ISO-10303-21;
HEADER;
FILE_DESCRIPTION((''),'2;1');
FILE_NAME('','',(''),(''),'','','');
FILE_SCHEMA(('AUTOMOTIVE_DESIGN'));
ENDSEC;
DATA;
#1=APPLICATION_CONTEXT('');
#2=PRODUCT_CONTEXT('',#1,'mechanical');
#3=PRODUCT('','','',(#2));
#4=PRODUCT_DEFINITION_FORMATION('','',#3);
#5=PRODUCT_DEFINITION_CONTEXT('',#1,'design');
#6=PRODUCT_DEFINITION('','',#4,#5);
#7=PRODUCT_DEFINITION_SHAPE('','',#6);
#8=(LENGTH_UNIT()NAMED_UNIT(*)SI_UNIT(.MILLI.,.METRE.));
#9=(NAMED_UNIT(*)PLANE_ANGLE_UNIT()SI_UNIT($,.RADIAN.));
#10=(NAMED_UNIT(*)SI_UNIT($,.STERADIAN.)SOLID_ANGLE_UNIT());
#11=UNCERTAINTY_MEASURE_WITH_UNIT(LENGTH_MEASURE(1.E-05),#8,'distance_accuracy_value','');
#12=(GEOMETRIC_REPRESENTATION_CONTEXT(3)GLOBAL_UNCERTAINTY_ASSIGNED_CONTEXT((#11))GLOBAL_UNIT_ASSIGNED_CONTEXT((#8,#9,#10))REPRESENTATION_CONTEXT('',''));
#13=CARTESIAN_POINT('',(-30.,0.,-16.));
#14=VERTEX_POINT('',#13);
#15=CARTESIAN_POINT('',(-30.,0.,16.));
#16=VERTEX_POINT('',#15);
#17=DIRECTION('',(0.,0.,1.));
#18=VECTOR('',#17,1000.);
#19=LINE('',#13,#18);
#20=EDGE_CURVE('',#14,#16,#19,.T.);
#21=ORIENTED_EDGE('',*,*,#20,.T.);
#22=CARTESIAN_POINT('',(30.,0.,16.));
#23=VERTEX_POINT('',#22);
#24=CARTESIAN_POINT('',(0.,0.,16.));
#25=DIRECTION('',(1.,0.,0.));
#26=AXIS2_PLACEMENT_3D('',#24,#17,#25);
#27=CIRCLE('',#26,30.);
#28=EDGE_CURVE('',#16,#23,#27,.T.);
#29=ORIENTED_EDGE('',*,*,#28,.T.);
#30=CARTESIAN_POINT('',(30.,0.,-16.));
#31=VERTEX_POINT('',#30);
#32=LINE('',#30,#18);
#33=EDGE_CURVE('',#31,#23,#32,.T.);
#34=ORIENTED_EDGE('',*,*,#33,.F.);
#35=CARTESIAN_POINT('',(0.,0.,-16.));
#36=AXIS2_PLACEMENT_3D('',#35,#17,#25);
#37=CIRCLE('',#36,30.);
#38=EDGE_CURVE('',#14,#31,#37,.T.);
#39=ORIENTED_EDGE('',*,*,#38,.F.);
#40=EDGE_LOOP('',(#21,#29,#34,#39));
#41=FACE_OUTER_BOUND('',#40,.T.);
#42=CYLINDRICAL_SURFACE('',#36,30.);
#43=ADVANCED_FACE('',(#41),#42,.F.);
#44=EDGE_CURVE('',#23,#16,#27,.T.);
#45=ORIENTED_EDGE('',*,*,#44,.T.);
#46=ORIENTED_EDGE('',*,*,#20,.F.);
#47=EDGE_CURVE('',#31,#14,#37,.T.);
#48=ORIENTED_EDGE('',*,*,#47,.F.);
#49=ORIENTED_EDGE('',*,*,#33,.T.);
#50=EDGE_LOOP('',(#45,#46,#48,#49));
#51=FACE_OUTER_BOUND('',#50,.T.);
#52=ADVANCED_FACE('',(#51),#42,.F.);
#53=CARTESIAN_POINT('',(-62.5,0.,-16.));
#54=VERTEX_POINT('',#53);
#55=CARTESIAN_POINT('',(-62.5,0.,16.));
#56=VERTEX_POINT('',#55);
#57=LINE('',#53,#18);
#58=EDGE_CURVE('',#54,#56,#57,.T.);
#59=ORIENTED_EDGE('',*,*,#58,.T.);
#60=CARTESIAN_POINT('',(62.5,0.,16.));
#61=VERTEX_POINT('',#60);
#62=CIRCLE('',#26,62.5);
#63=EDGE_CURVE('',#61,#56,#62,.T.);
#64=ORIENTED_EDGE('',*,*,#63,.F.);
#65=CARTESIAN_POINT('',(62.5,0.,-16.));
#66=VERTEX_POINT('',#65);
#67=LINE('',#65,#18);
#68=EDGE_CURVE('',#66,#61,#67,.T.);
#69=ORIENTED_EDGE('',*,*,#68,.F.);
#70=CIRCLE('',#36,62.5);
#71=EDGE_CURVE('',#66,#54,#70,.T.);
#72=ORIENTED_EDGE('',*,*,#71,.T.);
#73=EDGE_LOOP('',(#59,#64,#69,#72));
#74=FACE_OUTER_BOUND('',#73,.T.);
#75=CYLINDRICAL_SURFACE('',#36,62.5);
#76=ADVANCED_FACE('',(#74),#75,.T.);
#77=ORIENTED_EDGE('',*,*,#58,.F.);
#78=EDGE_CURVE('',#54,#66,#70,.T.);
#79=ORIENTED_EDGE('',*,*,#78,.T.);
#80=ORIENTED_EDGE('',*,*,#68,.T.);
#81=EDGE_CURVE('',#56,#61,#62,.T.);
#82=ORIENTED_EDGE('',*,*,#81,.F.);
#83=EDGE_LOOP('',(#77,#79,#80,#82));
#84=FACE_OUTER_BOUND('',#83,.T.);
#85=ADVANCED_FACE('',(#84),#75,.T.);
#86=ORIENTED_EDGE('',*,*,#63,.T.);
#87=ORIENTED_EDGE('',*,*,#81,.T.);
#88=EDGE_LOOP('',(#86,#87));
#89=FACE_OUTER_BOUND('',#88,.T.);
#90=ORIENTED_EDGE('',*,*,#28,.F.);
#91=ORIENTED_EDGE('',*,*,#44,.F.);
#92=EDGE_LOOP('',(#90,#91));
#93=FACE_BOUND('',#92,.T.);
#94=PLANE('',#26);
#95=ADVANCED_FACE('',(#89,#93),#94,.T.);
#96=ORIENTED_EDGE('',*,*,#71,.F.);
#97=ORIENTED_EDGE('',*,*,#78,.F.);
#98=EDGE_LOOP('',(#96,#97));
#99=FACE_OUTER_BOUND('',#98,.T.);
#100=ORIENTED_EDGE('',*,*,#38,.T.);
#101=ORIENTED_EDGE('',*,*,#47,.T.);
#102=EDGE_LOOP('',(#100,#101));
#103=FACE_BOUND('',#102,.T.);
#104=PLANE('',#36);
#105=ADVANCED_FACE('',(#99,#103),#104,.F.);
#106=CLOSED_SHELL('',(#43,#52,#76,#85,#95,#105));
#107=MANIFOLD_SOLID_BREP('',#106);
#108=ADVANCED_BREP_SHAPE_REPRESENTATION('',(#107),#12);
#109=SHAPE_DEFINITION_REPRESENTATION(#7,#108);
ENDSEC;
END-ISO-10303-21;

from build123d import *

# Parameters (mm, degrees)
SKETCH_1_R      = 62.5
SKETCH_1_R_2    = 30
EXTRUDE_1_DEPTH = 16


with BuildPart() as part:
    # 草图1 → 凸台-拉伸1 (new, symmetric)
    with BuildSketch(Plane.XY):
        Circle(SKETCH_1_R)
        Circle(SKETCH_1_R_2, mode=Mode.SUBTRACT)
    extrude(amount=EXTRUDE_1_DEPTH, both=True)


solid = part.part
